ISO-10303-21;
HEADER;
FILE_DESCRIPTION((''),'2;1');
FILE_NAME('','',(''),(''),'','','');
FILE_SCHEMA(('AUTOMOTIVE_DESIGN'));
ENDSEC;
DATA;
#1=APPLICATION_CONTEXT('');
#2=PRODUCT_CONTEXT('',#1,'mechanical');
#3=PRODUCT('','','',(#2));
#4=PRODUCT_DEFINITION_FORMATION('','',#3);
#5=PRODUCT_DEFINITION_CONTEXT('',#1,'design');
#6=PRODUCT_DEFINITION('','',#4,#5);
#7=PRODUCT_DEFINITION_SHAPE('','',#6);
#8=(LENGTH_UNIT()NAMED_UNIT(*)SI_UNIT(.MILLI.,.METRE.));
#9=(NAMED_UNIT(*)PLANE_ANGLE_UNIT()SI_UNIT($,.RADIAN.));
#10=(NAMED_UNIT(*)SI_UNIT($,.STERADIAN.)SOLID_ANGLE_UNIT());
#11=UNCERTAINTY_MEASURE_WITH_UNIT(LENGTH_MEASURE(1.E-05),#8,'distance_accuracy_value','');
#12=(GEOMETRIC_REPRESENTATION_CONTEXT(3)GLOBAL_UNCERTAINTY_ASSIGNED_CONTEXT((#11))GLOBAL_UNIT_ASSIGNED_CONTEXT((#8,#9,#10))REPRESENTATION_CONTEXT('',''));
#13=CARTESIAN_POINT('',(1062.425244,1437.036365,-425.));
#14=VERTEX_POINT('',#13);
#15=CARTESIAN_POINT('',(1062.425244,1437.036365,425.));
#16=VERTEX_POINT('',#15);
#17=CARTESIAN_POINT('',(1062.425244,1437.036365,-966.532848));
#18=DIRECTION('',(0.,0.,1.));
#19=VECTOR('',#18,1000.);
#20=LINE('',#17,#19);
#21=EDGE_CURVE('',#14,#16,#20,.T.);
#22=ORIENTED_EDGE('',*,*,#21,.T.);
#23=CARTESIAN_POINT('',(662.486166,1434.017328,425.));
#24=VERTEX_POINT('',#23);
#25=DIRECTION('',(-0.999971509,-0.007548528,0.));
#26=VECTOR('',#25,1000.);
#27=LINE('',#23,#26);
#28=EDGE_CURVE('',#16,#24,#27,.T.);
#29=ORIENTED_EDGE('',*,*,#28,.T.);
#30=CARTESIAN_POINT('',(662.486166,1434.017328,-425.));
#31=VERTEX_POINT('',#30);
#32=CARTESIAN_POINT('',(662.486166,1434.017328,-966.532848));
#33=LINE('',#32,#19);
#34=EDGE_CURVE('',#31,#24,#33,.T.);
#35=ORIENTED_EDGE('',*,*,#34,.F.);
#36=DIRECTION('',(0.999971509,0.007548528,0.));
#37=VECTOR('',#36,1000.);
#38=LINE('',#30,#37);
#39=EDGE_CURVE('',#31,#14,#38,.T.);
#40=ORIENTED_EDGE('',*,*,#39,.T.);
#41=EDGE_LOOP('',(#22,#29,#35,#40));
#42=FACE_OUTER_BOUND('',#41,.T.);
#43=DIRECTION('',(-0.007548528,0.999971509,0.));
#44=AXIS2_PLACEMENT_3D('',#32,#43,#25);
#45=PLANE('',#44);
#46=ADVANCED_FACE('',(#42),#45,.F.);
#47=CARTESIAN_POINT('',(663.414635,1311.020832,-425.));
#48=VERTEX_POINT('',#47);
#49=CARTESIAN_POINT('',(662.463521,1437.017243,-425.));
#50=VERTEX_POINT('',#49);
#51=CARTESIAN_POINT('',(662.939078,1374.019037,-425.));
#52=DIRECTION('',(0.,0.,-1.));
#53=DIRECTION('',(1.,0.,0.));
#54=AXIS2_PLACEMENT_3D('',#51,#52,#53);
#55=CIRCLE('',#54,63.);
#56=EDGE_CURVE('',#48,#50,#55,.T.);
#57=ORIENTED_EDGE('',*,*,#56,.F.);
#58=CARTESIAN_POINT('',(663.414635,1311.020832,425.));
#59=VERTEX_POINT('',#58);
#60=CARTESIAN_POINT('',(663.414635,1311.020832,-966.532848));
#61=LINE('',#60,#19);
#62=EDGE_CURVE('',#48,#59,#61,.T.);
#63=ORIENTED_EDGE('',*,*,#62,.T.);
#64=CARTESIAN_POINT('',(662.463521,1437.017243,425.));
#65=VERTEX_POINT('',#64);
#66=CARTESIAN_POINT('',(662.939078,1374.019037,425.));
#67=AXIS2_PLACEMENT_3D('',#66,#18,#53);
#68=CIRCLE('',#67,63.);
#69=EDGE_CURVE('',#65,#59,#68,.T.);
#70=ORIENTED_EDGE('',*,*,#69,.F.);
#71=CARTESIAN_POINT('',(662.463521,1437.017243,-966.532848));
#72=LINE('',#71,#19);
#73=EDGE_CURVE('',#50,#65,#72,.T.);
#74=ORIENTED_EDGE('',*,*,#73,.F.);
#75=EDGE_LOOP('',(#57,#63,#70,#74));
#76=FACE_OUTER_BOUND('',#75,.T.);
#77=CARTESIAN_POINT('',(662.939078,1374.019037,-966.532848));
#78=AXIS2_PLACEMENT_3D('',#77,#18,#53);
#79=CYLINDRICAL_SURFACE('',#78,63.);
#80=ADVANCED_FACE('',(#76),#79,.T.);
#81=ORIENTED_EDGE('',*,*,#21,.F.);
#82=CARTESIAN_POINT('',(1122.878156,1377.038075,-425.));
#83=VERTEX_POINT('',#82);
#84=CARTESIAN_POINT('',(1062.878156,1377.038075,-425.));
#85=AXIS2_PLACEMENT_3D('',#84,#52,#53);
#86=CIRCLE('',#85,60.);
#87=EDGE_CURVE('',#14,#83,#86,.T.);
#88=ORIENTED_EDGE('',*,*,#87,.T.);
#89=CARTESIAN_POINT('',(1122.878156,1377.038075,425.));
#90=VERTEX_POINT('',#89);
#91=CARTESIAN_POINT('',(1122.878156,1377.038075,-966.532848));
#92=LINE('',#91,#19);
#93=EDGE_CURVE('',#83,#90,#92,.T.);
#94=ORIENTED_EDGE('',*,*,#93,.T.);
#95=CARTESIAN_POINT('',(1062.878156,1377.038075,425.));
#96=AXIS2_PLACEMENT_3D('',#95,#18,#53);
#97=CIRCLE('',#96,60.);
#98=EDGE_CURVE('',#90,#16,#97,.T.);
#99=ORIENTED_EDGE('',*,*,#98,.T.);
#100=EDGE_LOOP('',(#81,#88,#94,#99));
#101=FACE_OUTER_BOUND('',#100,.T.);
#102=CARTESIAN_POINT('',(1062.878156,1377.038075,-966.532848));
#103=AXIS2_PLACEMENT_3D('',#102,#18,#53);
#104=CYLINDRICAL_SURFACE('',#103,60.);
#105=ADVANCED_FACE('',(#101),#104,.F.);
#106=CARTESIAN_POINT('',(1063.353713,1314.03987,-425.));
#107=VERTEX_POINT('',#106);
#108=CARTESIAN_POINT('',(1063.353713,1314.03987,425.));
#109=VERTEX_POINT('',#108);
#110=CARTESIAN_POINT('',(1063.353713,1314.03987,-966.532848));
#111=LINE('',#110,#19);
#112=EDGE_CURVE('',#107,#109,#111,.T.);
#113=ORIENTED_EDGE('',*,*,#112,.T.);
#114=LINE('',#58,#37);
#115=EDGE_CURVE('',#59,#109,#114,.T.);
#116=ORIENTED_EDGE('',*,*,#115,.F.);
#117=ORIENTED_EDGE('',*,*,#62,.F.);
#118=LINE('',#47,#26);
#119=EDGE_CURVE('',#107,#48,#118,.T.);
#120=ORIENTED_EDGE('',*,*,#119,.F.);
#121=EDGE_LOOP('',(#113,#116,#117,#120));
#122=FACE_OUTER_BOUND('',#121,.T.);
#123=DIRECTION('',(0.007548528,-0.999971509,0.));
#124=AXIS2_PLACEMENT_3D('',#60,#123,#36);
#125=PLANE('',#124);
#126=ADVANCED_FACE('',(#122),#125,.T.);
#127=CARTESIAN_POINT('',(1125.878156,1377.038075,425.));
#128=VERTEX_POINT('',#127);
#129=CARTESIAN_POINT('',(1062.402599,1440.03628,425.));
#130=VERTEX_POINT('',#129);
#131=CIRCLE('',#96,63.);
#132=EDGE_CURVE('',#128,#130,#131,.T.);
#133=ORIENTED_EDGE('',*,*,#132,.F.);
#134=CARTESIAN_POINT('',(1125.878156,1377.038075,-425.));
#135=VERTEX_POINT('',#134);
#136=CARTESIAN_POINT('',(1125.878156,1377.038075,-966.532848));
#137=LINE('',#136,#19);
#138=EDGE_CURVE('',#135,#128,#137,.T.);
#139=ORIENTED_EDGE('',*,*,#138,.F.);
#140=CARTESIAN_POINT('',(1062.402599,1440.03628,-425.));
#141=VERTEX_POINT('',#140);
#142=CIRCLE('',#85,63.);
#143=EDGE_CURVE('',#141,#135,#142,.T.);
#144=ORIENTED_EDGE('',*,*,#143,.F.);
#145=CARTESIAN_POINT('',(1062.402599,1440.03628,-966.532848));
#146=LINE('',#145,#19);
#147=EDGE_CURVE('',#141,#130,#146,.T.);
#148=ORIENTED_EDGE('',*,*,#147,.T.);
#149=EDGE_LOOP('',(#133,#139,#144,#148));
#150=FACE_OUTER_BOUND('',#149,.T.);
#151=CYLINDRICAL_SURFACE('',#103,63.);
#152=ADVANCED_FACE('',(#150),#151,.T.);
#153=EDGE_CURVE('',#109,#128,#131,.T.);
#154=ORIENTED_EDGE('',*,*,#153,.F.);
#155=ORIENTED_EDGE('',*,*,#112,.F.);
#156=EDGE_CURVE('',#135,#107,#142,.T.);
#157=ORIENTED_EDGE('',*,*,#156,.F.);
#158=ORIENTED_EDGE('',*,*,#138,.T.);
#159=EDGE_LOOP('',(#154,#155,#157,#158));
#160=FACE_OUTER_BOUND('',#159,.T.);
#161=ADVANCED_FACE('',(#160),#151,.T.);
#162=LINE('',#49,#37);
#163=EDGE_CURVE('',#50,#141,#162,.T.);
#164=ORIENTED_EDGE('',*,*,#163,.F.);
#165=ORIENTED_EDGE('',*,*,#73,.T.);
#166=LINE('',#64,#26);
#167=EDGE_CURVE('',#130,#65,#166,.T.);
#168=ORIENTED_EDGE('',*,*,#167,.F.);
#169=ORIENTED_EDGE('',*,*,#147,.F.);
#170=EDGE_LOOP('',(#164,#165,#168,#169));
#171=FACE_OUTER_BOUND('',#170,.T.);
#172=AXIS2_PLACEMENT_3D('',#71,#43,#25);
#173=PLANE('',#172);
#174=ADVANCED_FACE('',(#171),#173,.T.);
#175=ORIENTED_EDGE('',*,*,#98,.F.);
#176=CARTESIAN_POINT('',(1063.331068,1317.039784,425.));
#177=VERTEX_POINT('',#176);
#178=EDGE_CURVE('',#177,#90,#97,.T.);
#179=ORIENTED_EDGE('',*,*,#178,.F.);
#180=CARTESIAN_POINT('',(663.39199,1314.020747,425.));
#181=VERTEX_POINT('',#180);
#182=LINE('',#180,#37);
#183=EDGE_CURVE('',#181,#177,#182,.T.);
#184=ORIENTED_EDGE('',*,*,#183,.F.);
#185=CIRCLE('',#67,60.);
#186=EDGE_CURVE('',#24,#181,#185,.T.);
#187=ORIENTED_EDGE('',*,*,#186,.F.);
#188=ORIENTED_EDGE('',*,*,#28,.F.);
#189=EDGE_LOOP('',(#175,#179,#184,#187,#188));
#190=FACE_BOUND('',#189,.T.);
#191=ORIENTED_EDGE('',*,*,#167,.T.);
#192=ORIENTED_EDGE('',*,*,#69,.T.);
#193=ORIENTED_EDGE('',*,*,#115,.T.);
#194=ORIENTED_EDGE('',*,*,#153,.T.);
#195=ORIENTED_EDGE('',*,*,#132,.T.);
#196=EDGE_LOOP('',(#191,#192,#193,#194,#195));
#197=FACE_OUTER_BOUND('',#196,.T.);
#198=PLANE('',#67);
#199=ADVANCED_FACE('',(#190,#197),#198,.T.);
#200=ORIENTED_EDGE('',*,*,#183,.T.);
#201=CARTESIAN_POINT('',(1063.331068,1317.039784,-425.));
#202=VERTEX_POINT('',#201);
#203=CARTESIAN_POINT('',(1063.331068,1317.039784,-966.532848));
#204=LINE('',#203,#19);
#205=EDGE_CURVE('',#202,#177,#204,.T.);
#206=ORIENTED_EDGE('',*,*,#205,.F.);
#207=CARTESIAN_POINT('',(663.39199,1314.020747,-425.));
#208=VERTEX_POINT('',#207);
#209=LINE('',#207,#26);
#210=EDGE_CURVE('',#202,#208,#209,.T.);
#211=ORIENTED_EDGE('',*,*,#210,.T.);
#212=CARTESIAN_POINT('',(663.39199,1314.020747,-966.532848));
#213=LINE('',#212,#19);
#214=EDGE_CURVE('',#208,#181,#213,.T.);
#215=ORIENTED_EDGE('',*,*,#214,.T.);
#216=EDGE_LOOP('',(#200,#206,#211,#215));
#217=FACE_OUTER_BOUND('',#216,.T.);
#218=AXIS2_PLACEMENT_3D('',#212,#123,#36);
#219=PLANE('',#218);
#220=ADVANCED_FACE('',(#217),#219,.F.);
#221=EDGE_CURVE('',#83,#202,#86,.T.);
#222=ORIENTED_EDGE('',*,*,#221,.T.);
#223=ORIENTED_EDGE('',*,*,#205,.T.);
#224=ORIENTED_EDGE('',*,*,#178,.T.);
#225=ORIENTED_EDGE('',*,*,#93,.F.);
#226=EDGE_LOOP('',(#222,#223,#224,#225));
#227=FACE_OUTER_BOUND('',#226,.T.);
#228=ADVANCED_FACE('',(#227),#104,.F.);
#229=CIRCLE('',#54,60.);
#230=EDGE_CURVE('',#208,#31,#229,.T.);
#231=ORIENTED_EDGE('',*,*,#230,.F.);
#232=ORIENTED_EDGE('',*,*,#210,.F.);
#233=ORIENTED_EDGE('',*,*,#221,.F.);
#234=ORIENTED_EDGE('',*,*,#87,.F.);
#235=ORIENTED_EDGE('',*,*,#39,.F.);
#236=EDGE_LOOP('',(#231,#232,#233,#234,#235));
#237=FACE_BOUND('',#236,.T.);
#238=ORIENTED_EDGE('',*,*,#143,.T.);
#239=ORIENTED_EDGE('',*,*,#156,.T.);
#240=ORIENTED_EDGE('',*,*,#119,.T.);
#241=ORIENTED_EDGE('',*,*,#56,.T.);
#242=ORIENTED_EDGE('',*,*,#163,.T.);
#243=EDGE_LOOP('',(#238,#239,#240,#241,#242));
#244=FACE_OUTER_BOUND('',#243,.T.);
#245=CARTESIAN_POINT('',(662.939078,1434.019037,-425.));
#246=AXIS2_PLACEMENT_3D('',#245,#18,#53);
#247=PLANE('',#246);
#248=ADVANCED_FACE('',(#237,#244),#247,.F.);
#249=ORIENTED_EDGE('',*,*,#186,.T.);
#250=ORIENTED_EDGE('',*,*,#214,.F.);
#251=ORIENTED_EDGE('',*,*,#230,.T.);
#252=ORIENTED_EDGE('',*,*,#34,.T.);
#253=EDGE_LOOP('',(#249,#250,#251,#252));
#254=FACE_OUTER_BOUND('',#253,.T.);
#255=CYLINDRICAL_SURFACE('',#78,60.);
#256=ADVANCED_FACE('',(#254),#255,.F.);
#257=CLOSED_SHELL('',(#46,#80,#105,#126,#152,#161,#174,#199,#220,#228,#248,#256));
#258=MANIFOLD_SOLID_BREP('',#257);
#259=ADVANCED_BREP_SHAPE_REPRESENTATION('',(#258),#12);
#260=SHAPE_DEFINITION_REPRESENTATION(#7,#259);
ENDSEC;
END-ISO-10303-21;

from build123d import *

# Parameters (mm, degrees)
EXTRUDE_1_DEPTH = 850


with BuildPart() as part:
    # 草图1 → 凸台-拉伸1 (new body)
    with BuildSketch(Plane.XY.offset(425)):
        with BuildLine():
            Line((662.463520786, 1437.017242521), (1062.402598848, 1440.036279946))
            ThreePointArc((1062.402598848, 1440.036279946), (1125.876361221, 1377.513632127), (1063.353713402, 1314.039869754))
            Line((1063.353713402, 1314.039869754), (663.414635339, 1311.020832329))
            ThreePointArc((663.414635339, 1311.020832329), (599.940872967, 1373.543480148), (662.463520786, 1437.017242521))
        make_face()
        with BuildLine():
            Line((662.48616637, 1434.017327992), (1062.425244433, 1437.036365417))
            ThreePointArc((1062.425244433, 1437.036365417), (1122.876446692, 1377.490986542), (1063.331067817, 1317.039784283))
            Line((1063.331067817, 1317.039784283), (663.391989755, 1314.020746858))
            ThreePointArc((663.391989755, 1314.020746858), (602.940787495, 1373.566125733), (662.48616637, 1434.017327992))
        make_face(mode=Mode.SUBTRACT)
    extrude(amount=-EXTRUDE_1_DEPTH)


solid = part.part
